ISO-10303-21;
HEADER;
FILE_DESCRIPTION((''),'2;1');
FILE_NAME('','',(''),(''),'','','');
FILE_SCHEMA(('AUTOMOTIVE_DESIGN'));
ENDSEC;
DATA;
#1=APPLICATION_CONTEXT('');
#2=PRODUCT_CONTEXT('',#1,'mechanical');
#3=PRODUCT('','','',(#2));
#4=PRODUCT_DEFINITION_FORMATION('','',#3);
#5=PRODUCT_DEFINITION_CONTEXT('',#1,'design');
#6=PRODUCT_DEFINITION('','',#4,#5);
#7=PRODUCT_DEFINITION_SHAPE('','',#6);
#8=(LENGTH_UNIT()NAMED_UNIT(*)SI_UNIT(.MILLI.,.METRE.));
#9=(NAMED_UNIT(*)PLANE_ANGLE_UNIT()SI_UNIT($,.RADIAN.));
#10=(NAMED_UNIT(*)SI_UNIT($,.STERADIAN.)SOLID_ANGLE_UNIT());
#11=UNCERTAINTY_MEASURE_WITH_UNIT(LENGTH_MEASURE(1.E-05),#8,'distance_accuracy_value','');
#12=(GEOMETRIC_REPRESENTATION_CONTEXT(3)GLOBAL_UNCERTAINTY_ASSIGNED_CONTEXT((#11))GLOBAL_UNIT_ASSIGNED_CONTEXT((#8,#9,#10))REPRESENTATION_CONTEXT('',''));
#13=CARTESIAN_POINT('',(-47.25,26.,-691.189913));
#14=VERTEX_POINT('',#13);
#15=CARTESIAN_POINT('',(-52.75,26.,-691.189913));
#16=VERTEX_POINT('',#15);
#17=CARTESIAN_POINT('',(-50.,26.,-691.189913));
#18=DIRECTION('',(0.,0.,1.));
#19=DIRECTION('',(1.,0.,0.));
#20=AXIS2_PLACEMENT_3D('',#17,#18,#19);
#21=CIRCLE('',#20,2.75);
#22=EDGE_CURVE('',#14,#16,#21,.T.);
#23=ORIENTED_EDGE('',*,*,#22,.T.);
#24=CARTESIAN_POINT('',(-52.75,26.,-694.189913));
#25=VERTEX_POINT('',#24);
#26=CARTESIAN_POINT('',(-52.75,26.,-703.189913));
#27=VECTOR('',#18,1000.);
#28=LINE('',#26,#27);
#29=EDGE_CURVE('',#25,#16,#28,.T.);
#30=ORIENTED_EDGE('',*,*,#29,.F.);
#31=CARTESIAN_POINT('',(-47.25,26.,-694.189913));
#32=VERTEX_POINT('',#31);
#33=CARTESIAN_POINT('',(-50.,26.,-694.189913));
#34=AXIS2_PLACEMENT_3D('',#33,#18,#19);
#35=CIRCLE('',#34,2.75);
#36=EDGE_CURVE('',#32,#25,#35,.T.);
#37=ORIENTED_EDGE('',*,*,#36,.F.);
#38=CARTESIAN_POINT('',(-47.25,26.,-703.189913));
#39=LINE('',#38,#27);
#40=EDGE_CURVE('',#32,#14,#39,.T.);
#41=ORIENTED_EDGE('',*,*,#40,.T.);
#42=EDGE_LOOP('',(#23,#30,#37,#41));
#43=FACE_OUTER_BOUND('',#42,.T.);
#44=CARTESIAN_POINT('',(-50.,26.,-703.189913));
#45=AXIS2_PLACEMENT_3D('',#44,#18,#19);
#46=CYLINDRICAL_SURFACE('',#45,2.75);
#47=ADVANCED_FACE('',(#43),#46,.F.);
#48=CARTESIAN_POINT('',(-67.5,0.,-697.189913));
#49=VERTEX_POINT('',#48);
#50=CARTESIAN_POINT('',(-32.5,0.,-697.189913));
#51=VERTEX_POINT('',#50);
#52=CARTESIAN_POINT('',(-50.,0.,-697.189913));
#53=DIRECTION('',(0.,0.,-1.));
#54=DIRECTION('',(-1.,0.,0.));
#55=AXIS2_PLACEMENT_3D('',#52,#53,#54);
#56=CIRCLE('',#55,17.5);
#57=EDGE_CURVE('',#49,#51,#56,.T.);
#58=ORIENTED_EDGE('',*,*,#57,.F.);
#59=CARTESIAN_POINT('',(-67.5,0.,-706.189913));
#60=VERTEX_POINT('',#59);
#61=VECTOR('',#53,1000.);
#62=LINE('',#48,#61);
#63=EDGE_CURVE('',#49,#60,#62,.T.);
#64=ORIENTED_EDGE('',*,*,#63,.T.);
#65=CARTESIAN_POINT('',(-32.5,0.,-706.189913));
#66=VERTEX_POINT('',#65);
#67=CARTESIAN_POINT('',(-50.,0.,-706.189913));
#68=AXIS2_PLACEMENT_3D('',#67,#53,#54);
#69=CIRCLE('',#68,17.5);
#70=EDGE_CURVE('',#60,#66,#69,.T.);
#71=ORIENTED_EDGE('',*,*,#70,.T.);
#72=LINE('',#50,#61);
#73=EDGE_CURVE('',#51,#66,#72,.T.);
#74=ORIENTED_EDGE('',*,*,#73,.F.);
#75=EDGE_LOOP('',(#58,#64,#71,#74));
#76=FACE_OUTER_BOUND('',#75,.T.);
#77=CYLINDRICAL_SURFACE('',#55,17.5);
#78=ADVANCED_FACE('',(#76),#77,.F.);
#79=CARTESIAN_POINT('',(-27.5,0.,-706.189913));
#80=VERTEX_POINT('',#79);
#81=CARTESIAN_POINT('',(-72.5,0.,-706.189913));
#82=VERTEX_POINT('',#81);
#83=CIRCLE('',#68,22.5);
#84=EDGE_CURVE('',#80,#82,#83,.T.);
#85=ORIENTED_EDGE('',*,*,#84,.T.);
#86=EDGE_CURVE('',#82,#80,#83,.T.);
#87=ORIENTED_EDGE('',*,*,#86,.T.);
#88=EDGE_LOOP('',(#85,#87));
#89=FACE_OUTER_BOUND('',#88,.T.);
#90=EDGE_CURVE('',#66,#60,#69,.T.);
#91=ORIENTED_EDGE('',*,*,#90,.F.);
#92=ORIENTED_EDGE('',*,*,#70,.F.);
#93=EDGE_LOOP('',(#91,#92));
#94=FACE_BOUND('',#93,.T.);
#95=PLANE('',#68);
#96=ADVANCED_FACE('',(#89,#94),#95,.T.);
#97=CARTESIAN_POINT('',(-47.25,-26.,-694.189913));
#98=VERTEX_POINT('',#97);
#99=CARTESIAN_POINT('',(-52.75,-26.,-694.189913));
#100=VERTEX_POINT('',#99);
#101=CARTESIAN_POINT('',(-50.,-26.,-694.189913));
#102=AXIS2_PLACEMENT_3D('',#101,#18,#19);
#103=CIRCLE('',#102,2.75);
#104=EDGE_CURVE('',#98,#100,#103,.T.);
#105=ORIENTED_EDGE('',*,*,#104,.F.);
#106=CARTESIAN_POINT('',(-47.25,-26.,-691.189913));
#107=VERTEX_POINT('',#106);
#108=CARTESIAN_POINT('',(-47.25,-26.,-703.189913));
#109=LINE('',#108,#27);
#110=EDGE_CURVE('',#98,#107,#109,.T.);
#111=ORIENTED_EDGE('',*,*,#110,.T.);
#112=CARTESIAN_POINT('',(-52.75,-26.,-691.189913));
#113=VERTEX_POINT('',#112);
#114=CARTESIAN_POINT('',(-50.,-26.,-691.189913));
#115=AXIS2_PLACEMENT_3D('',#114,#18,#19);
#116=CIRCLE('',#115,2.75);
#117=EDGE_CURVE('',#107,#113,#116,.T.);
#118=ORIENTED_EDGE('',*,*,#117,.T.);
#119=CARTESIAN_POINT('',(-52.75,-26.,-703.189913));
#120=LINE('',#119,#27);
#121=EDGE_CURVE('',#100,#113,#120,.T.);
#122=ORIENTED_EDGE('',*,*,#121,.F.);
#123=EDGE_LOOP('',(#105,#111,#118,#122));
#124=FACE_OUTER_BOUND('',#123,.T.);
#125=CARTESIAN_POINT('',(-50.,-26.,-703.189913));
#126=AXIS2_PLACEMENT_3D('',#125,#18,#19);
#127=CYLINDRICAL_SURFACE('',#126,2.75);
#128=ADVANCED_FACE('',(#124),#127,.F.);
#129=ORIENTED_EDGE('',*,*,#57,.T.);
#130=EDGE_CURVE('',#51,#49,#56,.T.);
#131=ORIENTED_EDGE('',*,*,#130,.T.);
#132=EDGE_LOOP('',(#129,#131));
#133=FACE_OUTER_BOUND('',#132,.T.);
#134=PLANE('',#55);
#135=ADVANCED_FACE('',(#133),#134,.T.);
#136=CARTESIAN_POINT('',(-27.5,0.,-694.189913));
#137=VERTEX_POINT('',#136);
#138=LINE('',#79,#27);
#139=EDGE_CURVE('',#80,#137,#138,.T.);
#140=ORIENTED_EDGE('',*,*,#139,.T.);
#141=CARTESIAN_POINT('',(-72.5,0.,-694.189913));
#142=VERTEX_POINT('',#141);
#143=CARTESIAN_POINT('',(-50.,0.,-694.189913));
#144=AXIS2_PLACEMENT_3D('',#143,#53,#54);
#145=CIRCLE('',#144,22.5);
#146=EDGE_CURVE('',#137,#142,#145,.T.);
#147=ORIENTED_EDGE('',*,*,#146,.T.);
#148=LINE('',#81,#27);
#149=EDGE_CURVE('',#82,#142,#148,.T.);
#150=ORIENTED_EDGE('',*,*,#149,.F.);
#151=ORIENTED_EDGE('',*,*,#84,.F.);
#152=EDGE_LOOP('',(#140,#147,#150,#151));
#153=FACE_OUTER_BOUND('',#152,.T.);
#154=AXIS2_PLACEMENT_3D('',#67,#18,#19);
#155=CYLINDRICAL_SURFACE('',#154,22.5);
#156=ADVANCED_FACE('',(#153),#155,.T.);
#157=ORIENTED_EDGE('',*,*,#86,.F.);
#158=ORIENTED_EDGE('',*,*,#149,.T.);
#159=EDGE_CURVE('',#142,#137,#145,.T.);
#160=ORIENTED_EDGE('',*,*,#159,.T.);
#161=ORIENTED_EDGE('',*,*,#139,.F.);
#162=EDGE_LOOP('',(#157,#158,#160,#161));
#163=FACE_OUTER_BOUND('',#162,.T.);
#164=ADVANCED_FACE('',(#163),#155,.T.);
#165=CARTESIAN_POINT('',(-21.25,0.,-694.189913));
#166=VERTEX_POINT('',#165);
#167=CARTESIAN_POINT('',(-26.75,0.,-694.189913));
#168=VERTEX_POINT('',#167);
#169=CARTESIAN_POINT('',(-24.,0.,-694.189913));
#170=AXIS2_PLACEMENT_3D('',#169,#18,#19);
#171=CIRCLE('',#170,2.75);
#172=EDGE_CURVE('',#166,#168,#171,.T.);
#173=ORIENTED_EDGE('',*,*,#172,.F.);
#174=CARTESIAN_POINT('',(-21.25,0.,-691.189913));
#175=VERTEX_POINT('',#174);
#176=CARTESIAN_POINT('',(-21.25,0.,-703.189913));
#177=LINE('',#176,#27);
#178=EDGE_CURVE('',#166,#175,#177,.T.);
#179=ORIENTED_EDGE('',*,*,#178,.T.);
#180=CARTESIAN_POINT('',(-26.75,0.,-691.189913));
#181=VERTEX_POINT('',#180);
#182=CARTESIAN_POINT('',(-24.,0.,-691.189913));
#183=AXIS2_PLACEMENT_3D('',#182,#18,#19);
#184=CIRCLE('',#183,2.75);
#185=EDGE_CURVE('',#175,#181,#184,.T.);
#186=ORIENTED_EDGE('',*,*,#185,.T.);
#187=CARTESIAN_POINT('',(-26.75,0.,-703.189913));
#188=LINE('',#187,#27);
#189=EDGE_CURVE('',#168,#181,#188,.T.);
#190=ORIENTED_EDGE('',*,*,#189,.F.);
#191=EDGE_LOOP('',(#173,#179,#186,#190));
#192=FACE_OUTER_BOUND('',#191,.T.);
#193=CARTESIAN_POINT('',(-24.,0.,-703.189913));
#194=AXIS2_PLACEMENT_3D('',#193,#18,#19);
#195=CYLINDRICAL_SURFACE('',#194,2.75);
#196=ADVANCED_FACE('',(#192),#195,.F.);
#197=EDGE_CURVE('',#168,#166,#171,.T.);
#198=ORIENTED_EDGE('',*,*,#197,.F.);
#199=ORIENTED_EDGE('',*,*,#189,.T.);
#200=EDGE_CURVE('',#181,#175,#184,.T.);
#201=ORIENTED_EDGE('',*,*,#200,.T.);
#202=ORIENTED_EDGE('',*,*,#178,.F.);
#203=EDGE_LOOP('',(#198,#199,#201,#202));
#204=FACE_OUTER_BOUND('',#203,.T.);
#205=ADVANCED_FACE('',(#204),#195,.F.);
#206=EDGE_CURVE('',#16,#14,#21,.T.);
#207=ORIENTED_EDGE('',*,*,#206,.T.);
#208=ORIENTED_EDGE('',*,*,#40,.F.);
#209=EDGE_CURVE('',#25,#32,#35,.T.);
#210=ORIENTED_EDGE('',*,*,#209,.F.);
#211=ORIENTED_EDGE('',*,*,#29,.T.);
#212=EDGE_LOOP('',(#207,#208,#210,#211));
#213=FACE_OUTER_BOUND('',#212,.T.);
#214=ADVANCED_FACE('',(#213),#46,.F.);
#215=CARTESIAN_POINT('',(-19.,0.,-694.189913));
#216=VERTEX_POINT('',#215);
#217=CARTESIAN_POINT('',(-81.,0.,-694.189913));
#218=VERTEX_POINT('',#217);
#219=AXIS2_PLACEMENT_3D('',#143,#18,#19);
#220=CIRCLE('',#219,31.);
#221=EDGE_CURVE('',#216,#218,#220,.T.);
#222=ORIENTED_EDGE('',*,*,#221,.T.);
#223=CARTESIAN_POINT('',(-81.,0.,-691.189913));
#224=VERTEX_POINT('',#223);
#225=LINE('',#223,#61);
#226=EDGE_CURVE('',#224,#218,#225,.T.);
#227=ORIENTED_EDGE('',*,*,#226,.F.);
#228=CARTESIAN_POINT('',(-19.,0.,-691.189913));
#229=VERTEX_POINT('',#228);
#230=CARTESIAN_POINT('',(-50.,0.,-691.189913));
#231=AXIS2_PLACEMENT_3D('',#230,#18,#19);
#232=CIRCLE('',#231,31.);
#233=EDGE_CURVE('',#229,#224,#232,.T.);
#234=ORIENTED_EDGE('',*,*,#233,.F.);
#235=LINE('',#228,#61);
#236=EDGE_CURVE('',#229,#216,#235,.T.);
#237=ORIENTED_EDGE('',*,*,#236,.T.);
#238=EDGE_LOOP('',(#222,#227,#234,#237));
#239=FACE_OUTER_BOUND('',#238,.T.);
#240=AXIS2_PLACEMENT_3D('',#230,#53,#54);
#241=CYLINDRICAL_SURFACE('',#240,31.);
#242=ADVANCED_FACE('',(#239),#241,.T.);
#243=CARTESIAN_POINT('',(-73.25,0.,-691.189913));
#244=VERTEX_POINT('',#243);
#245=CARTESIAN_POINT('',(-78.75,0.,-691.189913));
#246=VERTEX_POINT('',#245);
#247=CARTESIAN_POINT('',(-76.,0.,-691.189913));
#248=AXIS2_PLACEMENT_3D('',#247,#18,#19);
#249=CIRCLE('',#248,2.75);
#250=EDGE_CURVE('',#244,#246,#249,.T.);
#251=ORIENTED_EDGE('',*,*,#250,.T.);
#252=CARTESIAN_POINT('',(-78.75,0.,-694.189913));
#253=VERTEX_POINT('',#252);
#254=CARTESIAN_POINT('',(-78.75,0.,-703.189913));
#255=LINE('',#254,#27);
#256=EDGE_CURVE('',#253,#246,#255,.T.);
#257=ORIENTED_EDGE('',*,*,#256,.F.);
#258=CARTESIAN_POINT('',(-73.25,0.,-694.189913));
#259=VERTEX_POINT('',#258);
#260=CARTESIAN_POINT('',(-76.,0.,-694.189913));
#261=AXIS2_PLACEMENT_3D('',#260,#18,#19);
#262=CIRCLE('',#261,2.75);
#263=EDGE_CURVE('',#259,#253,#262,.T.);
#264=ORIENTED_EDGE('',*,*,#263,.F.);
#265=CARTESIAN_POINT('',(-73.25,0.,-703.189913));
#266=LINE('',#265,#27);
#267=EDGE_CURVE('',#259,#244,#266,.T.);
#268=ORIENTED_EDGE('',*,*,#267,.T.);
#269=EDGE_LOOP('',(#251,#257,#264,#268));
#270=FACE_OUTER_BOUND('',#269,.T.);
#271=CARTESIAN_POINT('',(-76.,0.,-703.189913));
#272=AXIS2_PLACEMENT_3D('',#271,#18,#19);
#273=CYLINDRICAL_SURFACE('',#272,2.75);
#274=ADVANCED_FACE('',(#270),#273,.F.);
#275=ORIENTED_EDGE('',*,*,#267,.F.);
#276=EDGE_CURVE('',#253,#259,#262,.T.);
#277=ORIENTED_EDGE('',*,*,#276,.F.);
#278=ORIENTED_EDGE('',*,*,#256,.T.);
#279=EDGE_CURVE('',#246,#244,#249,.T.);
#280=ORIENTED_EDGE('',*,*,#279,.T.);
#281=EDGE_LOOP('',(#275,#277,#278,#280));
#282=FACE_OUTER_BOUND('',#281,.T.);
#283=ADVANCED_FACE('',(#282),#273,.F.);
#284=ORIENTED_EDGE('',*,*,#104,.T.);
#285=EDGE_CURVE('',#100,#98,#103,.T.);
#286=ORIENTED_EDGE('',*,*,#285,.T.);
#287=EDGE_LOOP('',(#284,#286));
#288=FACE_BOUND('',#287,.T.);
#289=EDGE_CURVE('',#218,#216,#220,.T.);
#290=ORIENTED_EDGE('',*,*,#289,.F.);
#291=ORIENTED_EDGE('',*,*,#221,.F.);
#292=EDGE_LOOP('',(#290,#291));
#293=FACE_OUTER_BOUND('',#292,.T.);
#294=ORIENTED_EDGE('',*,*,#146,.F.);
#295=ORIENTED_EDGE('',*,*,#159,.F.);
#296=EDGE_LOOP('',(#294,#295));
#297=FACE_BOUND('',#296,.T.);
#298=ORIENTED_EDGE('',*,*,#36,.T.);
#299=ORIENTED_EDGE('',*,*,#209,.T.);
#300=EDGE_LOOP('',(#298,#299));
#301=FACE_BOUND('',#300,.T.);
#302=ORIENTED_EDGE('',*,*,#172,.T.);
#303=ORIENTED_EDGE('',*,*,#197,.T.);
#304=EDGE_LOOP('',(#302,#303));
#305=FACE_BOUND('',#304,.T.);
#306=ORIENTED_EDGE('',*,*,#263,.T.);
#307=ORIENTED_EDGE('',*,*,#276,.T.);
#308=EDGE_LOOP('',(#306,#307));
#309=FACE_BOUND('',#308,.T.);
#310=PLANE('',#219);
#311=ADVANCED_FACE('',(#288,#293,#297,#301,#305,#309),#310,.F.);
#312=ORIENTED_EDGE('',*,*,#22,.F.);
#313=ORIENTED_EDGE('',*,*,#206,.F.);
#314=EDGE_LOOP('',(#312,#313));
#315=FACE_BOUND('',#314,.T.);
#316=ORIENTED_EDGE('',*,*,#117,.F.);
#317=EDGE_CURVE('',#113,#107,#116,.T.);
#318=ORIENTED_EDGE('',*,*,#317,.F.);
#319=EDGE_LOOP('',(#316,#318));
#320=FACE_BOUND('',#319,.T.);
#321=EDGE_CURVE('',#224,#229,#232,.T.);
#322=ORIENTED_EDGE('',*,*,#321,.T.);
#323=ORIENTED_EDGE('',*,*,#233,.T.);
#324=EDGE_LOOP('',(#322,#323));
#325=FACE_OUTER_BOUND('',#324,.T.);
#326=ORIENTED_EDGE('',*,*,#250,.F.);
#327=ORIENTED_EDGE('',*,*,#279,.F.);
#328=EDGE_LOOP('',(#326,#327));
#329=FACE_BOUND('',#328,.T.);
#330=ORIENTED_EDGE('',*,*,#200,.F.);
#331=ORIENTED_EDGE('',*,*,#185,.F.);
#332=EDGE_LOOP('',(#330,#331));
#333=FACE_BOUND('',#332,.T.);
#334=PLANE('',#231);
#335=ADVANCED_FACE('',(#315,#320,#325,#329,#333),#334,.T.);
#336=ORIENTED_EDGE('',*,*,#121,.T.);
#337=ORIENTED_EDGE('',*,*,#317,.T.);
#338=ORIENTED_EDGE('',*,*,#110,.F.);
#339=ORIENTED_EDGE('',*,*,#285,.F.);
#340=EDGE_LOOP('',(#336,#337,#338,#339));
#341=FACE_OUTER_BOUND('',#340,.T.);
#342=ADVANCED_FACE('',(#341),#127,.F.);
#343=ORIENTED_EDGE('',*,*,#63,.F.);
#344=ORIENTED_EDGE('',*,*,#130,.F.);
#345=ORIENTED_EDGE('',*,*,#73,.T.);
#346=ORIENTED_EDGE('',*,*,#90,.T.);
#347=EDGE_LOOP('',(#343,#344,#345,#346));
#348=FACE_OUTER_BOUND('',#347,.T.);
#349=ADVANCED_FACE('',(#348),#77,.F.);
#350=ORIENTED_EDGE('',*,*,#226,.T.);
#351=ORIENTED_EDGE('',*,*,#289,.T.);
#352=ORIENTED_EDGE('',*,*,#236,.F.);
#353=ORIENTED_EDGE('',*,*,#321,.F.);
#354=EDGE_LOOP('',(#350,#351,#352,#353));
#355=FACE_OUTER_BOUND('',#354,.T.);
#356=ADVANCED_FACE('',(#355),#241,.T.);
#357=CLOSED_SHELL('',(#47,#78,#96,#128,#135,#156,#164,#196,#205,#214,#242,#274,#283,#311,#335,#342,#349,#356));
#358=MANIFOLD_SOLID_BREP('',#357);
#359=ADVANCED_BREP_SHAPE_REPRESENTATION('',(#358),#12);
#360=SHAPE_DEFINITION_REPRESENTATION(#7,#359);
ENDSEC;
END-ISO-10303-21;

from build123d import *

# Parameters (mm, degrees)
SKETCH2_R           = 31
BOSS_EXTRUDE1_DEPTH = 3
SKETCH3_R           = 22.5
BOSS_EXTRUDE2_DEPTH = 12
SKETCH4_R           = 17.5
CUT_EXTRUDE1_DEPTH  = 9
SKETCH6_R           = 2.75
CUT_EXTRUDE2_DEPTH  = 12


with BuildPart() as part:
    # Sketch2 → Boss-Extrude1 (new body)
    with BuildSketch(Plane.XY.offset(-694.189912682)):
        with Locations((-50, 0)):
            Circle(SKETCH2_R)
    extrude(amount=BOSS_EXTRUDE1_DEPTH)

    # Sketch3 → Boss-Extrude2 (add)
    with BuildSketch(Plane(origin=(0, 0, -694.189912682), x_dir=(-1, 0, 0), z_dir=(0, 0, -1))):
        with Locations((50, 0)):
            Circle(SKETCH3_R)
    extrude(amount=BOSS_EXTRUDE2_DEPTH)

    # Sketch4 → Cut-Extrude1 (cut)
    with BuildSketch(Plane(origin=(0, 0, -706.189912682), x_dir=(-1, 0, 0), z_dir=(0, 0, -1))):
        with Locations((50, 0)):
            Circle(SKETCH4_R)
    extrude(amount=-CUT_EXTRUDE1_DEPTH, mode=Mode.SUBTRACT)

    # Sketch6 → Cut-Extrude2 (cut)
    with BuildSketch(Plane.XY.offset(-691.189912682)):
        with Locations((-50, 26)):
            Circle(SKETCH6_R)
        with Locations((-24, 0)):
            Circle(SKETCH6_R)
        with Locations((-50, -26)):
            Circle(SKETCH6_R)
        with Locations((-76, 0)):
            Circle(SKETCH6_R)
    extrude(amount=-CUT_EXTRUDE2_DEPTH, mode=Mode.SUBTRACT)


solid = part.part
